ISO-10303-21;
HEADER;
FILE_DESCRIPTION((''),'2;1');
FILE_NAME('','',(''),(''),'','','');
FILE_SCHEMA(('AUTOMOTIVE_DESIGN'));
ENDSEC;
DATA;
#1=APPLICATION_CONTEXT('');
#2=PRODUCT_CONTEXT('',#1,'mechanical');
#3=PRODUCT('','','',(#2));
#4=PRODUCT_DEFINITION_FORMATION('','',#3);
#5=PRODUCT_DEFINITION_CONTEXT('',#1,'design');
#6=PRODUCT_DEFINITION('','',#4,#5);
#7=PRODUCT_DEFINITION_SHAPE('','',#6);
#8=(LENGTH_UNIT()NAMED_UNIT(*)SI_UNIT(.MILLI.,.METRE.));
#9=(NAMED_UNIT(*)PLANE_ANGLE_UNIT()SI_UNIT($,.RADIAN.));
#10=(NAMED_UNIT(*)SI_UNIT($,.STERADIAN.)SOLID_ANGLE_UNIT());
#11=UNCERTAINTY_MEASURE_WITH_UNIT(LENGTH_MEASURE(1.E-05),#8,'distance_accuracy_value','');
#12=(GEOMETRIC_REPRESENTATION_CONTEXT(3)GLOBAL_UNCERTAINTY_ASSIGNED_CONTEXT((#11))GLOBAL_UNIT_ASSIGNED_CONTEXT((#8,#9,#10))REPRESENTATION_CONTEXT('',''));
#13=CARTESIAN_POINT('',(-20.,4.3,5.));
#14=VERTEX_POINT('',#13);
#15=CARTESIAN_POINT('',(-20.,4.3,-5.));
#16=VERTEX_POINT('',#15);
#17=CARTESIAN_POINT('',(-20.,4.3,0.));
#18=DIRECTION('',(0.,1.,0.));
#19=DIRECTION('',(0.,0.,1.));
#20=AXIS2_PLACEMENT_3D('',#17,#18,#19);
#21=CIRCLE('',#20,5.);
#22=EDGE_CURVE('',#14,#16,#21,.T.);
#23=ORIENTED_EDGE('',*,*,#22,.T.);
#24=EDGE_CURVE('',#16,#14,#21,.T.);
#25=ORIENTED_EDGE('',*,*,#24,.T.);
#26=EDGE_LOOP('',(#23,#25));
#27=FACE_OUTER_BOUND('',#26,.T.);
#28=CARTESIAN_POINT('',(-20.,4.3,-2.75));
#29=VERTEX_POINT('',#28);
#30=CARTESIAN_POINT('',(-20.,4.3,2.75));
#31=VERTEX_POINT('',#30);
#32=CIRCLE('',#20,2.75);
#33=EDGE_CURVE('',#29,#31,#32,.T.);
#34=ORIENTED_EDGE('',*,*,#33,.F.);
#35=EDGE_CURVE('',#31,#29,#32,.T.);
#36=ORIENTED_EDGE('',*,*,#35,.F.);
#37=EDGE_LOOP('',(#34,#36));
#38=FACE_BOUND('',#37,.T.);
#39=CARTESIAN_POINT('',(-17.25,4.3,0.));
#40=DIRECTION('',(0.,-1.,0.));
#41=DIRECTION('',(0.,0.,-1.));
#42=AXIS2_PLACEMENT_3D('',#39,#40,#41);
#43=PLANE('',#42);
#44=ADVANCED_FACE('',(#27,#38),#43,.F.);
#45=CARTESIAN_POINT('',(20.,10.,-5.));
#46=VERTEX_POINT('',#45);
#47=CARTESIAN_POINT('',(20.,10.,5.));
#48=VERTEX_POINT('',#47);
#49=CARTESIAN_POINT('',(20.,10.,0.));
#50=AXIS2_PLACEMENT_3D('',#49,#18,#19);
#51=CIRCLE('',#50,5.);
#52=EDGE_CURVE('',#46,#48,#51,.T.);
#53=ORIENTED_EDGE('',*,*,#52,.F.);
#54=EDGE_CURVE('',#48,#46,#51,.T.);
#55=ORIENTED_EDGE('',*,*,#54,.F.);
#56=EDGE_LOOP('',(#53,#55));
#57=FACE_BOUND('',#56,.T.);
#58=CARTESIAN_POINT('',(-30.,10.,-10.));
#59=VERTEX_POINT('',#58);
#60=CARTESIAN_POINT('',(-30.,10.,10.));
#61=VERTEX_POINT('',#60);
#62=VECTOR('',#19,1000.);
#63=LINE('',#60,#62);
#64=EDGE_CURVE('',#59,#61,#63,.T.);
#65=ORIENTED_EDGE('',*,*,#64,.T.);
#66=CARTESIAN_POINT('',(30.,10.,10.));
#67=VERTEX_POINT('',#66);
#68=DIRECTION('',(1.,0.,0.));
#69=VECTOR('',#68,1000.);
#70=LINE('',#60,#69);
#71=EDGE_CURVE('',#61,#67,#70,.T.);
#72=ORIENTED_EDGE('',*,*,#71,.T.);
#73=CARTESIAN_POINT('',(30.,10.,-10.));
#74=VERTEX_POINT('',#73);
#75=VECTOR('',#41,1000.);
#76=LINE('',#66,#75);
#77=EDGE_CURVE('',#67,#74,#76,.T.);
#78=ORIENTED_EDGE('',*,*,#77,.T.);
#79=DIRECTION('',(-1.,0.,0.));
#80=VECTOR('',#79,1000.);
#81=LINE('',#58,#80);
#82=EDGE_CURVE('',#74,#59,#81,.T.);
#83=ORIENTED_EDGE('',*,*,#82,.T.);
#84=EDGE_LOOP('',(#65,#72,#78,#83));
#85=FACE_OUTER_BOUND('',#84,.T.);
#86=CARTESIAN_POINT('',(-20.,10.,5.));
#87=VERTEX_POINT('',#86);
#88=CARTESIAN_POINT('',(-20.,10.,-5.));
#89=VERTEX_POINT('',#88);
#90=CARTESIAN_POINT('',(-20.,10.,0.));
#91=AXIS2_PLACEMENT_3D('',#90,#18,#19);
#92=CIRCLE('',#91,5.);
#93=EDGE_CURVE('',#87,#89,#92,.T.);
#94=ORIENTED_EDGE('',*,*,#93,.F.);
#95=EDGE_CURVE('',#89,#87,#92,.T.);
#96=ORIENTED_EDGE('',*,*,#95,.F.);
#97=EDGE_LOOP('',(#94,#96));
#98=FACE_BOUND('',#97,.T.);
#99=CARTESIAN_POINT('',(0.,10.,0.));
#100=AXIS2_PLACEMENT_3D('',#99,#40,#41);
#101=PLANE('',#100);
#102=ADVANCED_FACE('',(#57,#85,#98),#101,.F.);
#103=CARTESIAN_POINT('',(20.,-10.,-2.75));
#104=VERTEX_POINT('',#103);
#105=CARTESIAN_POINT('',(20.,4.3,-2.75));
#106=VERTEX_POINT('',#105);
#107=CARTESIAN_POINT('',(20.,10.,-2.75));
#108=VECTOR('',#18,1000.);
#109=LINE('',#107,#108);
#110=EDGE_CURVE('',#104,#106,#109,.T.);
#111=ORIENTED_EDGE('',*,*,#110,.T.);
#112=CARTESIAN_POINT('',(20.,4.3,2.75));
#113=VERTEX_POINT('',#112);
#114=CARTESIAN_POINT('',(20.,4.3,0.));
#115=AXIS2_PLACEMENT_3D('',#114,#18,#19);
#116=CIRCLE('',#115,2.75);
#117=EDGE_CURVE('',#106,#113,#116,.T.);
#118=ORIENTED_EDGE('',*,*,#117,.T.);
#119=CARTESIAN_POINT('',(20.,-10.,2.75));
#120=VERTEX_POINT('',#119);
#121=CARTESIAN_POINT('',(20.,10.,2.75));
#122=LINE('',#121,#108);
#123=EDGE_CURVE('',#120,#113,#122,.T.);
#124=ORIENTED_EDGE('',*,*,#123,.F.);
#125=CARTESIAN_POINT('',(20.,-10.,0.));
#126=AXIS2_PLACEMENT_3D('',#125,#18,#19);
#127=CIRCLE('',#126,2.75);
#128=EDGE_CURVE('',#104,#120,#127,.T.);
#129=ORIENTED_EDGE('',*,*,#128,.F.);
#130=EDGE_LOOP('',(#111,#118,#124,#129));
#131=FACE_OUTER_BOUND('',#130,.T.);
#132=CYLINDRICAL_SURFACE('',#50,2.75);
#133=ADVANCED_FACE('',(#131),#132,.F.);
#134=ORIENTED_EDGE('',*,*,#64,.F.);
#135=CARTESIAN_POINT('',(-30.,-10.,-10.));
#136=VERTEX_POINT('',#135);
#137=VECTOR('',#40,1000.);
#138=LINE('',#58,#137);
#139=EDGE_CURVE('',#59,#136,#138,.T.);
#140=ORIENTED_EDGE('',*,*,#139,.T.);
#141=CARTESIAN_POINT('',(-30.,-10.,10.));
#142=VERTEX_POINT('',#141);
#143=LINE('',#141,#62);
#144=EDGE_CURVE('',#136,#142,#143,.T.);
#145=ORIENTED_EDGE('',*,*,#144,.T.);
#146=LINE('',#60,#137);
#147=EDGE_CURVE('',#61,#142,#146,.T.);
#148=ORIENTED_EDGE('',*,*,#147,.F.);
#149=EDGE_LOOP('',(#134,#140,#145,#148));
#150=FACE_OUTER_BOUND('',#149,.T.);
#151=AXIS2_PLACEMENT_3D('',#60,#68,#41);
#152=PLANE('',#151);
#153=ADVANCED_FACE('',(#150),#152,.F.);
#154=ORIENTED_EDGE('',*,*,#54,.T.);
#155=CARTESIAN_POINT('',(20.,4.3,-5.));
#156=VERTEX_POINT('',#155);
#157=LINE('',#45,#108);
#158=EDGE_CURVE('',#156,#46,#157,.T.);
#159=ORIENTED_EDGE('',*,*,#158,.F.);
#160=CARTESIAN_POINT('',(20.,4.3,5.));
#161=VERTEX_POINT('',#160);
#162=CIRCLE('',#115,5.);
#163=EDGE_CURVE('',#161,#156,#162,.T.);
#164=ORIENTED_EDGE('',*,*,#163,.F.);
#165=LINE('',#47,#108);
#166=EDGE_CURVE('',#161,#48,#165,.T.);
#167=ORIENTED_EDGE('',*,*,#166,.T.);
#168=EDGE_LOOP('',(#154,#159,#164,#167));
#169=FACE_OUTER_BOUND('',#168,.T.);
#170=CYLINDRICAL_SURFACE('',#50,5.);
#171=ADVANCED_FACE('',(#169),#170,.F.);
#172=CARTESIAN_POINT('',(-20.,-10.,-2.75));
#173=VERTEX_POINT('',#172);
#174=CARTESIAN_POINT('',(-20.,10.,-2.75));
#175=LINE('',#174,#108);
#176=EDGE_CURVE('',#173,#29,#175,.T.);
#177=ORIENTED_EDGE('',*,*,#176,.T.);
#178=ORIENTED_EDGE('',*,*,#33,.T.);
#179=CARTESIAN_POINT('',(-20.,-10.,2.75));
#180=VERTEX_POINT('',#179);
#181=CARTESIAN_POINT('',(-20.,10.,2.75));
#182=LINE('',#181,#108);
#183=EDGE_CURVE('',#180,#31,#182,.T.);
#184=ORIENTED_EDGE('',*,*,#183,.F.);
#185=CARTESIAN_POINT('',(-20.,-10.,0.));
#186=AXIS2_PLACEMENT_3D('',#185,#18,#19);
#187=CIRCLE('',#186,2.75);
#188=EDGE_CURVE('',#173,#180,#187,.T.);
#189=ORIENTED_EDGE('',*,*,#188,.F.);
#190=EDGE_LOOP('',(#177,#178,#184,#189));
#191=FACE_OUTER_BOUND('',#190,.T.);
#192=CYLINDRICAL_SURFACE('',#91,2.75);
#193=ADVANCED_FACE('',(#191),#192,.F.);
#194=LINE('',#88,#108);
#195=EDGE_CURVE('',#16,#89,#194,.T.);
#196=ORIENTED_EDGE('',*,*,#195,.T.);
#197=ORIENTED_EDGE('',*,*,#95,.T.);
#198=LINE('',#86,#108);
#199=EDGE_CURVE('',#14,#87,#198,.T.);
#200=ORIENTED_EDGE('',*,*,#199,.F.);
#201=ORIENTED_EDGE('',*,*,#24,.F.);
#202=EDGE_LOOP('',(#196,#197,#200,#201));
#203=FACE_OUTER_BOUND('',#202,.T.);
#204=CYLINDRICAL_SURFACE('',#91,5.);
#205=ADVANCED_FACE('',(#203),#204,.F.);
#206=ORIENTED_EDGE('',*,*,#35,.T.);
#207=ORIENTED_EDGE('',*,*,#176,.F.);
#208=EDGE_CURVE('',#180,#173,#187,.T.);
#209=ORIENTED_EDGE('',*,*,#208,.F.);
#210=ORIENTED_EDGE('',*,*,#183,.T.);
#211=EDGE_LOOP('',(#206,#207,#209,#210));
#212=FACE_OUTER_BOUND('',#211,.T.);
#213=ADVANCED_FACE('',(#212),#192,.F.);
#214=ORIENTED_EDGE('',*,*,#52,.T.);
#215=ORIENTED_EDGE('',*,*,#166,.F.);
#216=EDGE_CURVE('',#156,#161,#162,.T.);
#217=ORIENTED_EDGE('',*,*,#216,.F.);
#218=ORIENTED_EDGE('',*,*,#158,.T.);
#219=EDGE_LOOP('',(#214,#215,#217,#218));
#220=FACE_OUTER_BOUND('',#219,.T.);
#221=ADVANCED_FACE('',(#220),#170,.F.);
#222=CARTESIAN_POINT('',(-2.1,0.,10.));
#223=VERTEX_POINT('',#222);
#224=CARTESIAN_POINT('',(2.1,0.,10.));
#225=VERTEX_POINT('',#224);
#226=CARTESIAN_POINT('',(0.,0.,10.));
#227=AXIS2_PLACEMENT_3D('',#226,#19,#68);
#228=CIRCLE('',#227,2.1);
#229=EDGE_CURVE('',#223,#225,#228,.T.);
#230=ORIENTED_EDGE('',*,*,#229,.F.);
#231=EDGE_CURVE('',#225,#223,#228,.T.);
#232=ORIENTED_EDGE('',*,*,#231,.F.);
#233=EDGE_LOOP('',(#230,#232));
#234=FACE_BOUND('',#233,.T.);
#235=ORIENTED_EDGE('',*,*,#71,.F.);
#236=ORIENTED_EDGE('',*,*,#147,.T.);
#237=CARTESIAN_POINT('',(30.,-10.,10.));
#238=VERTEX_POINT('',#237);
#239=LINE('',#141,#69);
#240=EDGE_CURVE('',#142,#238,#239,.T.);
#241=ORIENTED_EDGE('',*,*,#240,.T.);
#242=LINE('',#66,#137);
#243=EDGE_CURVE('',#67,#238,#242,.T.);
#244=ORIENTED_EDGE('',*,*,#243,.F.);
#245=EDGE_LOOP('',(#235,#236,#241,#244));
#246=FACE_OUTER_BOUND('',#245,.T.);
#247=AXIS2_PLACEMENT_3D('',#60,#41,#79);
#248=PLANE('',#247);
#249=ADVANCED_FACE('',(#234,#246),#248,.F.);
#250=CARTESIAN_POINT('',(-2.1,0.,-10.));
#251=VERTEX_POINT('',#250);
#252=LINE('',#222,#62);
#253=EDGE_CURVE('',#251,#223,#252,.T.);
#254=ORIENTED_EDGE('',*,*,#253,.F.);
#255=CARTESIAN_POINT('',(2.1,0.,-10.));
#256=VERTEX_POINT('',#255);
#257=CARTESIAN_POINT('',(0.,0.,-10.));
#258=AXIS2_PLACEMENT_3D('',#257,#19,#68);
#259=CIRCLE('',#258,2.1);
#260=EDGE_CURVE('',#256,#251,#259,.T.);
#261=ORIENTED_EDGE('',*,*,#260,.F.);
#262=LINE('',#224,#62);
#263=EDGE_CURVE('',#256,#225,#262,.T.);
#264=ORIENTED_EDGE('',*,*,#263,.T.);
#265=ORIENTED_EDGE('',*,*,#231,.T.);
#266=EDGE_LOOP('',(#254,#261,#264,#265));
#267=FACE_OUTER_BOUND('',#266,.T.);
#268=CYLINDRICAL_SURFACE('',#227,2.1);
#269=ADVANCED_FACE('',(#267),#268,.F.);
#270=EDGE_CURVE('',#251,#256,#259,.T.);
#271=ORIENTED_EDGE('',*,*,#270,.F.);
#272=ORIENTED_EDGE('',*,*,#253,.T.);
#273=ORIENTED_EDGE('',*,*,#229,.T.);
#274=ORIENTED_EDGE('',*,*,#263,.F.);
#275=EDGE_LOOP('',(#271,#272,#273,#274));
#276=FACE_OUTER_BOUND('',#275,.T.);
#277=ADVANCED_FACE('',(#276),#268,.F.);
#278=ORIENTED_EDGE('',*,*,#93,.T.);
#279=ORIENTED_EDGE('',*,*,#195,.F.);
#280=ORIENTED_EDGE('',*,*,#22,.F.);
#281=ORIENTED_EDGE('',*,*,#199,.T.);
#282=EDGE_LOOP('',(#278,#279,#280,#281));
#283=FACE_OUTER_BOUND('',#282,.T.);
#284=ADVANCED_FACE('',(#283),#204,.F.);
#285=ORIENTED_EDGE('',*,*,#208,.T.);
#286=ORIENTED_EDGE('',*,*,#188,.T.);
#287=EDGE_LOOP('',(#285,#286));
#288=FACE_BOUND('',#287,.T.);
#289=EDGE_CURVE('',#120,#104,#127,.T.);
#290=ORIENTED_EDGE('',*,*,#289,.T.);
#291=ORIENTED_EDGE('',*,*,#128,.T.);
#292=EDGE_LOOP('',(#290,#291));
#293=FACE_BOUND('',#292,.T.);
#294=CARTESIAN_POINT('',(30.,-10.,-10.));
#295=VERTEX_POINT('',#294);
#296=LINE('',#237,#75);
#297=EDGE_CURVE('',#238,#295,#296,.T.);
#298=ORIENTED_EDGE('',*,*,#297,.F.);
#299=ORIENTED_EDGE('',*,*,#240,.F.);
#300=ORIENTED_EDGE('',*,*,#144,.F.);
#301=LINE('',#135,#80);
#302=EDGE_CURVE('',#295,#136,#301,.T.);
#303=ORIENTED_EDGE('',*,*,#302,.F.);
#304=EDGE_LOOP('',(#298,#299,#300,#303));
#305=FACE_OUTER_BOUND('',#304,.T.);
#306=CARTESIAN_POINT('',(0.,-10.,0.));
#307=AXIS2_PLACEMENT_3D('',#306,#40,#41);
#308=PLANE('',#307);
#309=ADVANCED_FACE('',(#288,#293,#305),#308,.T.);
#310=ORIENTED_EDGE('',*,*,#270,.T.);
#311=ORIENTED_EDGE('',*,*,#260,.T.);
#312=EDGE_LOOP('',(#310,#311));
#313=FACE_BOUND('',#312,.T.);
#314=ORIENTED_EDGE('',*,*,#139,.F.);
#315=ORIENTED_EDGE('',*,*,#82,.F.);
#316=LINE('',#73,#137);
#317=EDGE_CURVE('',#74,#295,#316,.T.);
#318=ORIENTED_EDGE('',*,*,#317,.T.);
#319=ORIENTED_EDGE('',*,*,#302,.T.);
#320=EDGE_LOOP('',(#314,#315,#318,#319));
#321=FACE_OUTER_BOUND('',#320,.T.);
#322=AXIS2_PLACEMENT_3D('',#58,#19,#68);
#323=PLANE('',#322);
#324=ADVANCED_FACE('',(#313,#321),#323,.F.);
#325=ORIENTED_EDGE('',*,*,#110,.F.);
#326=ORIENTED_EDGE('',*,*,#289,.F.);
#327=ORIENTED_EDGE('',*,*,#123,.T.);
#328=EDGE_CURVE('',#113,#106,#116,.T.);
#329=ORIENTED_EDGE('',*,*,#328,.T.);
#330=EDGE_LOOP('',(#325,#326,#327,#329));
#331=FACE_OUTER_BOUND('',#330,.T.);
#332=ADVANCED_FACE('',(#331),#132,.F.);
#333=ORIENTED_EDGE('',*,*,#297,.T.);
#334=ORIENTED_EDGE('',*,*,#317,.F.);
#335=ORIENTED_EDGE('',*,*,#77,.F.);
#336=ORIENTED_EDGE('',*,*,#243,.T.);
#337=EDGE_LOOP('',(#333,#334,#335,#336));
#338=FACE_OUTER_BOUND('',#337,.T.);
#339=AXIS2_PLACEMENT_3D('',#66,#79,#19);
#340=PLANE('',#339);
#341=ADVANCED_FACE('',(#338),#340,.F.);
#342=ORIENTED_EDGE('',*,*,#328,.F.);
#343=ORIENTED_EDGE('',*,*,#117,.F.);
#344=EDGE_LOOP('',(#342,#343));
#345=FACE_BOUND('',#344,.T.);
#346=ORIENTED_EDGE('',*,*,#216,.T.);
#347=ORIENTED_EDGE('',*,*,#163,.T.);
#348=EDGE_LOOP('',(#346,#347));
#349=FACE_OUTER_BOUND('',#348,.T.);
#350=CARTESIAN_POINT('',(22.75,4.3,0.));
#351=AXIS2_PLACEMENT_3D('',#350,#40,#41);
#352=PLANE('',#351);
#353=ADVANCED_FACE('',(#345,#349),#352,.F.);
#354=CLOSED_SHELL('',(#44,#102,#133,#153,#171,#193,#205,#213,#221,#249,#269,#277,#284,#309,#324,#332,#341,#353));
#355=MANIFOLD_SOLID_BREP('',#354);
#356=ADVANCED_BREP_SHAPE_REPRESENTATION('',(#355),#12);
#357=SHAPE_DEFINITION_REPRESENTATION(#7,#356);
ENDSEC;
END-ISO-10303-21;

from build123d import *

# Parameters (mm, degrees)
SKETCH_1_W                = 60
SKETCH_1_H                = 20
EXTRUDE_1_DEPTH           = 10
HOLE_WIZARD_1_D           = 5.5
HOLE_WIZARD_1_CBORE_D     = 10
HOLE_WIZARD_1_CBORE_DEPTH = 5.7
HOLE_WIZARD_M5_1_D        = 4.2


with BuildPart() as part:
    # 草图1 → 凸台-拉伸1 (new, symmetric)
    with BuildSketch(Plane(origin=(0, 0, 0), x_dir=(1, 0, 0), z_dir=(0, 1, 0))):
        Rectangle(SKETCH_1_W, SKETCH_1_H)
    extrude(amount=EXTRUDE_1_DEPTH, both=True)

    # 打孔尺寸(%根据)内六角圆柱头螺钉的类型1 (through all)
    with Locations(Plane(origin=(0, 10, 0), x_dir=(1, 0, 0), z_dir=(0, 1, 0))):
        with Locations((20, 0), (-20, 0)):
            CounterBoreHole(HOLE_WIZARD_1_D / 2, HOLE_WIZARD_1_CBORE_D / 2, HOLE_WIZARD_1_CBORE_DEPTH)

    # M5 螺纹孔1 (through all)
    with Locations(Plane.XY.offset(10)):
        with Locations((0, 0)):
            Hole(HOLE_WIZARD_M5_1_D / 2)


solid = part.part
